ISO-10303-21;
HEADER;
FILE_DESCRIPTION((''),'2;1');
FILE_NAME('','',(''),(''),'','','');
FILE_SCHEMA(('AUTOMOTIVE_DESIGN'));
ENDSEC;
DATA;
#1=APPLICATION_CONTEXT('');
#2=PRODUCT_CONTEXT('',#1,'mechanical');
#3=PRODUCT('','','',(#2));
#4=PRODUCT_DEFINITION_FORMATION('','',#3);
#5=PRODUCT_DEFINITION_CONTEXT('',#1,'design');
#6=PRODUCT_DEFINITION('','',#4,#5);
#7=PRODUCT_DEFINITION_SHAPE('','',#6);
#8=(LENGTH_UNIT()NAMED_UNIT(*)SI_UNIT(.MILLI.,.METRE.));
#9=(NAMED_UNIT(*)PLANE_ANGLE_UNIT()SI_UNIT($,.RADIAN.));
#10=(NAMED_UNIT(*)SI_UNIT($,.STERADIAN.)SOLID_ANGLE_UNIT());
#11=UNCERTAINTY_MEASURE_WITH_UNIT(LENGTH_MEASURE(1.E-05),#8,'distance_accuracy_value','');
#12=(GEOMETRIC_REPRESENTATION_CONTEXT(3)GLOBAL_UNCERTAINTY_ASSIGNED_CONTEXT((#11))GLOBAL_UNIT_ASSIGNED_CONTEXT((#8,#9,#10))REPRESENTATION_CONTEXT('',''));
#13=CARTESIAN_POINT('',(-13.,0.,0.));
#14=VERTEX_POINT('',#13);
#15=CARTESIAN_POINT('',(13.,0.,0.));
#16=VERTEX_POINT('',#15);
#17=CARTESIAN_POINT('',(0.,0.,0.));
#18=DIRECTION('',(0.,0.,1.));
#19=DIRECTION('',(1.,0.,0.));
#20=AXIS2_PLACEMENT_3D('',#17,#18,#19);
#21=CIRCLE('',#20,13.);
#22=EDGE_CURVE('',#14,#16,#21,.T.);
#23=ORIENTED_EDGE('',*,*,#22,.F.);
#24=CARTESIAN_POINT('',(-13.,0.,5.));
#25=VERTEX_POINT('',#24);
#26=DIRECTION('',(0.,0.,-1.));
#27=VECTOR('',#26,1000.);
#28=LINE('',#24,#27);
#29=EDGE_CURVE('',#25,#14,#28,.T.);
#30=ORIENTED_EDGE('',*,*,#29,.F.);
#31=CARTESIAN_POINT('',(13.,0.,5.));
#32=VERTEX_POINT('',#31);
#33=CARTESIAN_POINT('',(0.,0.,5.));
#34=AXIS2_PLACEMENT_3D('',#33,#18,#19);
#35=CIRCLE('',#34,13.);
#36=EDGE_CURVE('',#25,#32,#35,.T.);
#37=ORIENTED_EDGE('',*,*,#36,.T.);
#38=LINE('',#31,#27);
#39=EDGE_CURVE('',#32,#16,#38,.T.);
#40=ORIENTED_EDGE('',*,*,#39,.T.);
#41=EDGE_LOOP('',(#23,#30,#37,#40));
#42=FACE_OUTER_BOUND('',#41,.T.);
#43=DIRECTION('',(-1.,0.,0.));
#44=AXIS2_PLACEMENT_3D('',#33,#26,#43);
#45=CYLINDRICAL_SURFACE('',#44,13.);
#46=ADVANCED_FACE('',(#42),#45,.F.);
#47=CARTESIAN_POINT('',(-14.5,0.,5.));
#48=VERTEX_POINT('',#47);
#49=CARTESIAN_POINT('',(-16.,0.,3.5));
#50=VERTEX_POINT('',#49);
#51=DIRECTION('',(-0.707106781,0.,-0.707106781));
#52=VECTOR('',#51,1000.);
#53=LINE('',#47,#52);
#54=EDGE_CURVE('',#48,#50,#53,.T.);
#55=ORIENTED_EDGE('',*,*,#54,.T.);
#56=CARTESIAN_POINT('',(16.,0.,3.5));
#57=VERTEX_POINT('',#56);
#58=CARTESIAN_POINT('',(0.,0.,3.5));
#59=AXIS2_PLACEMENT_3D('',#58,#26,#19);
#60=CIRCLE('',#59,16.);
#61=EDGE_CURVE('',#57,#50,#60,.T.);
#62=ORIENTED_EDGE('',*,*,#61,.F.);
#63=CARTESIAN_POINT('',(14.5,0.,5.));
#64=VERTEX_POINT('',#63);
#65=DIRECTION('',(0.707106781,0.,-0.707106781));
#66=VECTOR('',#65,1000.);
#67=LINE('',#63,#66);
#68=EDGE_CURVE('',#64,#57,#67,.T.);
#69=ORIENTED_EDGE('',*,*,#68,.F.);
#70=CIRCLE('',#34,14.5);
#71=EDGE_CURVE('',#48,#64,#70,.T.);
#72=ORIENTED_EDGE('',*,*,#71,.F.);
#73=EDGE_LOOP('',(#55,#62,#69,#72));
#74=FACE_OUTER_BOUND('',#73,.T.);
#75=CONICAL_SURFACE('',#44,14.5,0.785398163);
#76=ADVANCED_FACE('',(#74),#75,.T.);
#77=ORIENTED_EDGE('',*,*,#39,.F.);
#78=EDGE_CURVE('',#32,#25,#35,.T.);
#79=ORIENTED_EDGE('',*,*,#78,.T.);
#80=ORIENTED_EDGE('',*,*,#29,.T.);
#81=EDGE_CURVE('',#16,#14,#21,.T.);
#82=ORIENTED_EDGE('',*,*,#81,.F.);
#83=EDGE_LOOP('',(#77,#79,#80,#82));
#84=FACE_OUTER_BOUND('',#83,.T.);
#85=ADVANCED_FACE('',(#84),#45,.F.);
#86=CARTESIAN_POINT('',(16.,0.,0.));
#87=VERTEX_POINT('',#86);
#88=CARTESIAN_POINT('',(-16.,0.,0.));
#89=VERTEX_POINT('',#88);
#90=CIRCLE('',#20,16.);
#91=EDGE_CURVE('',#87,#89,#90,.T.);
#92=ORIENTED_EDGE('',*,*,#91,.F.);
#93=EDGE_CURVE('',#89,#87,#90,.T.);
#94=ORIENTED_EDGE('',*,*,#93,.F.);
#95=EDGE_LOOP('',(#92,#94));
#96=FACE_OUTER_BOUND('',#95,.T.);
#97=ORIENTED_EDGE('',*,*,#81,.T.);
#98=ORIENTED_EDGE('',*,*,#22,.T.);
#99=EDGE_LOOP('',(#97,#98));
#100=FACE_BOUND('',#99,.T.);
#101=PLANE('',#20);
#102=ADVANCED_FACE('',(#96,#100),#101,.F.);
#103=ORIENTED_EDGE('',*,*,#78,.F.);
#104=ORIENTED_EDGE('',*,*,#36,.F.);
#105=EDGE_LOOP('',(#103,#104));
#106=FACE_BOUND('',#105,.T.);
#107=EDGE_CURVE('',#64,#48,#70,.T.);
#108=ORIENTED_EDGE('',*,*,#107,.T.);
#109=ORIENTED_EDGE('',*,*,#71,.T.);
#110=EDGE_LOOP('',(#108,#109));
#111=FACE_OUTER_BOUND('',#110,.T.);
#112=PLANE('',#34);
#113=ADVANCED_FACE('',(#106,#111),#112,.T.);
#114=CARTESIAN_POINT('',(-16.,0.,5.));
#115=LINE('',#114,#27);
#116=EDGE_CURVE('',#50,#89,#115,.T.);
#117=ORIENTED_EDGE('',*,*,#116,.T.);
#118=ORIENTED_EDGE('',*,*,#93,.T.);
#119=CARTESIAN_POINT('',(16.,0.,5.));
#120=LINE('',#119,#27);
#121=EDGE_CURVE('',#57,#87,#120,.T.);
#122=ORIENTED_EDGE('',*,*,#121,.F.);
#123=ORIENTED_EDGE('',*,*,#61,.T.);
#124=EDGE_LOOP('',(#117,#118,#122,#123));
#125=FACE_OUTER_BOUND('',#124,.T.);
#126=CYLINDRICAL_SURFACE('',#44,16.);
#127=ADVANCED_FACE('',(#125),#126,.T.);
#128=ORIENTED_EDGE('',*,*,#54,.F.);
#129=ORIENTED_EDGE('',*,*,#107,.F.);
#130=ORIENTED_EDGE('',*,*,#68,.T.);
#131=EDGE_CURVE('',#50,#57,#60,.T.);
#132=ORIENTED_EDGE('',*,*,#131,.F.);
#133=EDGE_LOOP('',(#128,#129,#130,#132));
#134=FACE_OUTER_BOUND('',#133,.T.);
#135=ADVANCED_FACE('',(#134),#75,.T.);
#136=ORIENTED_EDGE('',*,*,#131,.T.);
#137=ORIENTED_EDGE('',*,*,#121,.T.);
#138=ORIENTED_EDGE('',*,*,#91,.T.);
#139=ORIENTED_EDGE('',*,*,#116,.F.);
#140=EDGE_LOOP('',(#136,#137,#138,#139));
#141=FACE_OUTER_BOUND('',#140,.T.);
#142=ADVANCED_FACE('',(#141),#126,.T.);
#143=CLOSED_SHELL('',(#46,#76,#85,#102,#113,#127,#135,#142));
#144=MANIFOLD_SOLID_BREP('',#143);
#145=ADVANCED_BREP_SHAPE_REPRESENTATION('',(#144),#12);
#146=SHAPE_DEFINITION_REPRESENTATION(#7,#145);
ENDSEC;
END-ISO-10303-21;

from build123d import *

# Parameters (mm, degrees)
SKETCH1_R           = 16
SKETCH1_R_2         = 13
BOSS_EXTRUDE1_DEPTH = 5
CHAMFER1_SIZE       = 1.5


with BuildPart() as part:
    # Sketch1 → Boss-Extrude1 (new body)
    with BuildSketch(Plane.XY):
        Circle(SKETCH1_R)
        Circle(SKETCH1_R_2, mode=Mode.SUBTRACT)
    extrude(amount=BOSS_EXTRUDE1_DEPTH)

    # Chamfer1
    chamfer1_edges = [part.edges().sort_by_distance(p)[0] for p in [
        (-16, 0, 5),
    ]]
    chamfer(chamfer1_edges, length=CHAMFER1_SIZE)


solid = part.part
